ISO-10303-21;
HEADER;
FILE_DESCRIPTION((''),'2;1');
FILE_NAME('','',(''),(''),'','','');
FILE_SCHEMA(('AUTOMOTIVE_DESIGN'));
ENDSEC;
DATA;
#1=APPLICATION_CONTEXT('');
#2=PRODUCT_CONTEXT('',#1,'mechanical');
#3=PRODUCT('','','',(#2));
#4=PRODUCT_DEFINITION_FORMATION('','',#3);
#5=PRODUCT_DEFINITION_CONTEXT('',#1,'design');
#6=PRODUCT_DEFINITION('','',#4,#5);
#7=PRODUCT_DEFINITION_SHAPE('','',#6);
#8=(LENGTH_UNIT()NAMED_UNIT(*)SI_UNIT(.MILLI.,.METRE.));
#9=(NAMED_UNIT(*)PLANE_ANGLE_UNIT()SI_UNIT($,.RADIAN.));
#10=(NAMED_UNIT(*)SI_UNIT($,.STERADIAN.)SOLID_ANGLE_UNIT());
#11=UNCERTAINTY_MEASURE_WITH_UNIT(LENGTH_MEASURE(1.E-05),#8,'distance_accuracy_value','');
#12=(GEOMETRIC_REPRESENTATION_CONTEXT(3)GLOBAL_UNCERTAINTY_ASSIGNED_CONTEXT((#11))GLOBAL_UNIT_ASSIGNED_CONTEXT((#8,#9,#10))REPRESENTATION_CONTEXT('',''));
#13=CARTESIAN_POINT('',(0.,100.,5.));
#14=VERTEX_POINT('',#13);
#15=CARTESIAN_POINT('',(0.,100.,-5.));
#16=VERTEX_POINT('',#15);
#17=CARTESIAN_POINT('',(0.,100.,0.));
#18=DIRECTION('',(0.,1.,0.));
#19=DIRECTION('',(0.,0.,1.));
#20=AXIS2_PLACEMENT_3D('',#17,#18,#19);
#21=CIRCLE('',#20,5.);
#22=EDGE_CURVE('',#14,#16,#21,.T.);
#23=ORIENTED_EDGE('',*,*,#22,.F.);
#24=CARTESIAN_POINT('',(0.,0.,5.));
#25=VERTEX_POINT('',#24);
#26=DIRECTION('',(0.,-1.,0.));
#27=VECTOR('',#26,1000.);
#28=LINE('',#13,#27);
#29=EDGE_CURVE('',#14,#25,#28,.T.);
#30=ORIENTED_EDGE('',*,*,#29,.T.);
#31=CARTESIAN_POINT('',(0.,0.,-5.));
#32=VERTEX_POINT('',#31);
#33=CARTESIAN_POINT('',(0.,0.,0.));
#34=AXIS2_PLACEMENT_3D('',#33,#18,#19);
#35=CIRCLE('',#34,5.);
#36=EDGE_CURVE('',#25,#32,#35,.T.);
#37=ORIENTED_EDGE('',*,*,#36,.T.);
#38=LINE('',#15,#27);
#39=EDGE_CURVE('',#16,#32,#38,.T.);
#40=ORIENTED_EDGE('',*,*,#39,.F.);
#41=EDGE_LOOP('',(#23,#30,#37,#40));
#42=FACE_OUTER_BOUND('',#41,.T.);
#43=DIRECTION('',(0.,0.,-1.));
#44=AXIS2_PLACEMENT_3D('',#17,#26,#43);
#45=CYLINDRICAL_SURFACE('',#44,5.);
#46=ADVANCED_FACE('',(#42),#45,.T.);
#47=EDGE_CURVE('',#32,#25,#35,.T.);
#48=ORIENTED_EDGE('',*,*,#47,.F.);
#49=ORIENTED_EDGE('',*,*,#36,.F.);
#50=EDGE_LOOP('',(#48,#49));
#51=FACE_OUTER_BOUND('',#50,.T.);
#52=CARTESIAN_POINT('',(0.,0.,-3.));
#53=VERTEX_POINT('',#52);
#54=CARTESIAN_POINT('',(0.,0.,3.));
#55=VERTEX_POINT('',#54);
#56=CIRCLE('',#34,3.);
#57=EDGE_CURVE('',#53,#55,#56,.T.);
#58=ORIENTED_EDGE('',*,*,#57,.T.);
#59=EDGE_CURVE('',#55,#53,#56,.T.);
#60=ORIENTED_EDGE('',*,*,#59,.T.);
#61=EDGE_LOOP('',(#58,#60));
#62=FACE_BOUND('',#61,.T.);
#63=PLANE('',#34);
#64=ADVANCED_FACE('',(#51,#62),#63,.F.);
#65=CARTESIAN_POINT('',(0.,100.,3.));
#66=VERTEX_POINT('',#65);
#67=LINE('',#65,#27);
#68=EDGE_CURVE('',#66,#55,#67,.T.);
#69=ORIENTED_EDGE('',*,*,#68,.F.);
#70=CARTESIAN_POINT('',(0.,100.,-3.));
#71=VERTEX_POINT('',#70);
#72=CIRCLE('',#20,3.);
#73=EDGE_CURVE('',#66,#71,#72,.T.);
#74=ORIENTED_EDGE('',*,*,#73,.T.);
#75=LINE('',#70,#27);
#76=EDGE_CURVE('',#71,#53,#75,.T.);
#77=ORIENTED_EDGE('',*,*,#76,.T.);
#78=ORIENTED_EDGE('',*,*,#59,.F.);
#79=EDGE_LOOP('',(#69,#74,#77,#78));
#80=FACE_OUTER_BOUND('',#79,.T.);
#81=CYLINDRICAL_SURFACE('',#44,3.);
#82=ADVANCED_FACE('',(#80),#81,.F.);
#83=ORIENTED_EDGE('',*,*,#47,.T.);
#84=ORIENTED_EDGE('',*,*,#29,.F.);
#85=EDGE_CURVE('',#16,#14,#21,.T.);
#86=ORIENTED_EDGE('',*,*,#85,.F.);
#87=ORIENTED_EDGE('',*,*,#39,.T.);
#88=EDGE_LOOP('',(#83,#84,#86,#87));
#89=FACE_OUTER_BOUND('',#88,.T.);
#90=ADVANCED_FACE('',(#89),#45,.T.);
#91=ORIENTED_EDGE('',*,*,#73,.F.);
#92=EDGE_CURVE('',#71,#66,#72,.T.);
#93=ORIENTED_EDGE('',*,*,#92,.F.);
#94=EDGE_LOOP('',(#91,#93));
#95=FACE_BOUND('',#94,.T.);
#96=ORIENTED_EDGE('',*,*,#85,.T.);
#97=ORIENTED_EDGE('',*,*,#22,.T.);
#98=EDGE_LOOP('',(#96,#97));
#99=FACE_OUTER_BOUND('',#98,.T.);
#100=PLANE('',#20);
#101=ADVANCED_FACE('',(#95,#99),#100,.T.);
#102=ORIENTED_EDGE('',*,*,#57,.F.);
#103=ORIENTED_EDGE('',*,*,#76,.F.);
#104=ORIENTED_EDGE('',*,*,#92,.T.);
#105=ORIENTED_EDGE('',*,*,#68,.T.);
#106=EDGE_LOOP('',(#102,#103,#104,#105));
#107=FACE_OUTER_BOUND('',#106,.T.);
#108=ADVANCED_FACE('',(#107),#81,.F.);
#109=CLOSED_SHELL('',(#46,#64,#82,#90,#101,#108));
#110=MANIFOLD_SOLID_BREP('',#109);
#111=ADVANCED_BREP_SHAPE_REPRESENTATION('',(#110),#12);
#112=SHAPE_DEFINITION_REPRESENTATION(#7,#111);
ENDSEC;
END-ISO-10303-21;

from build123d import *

# Parameters (mm, degrees)
SKETCH_1_R      = 5
SKETCH_1_R_2    = 3
EXTRUDE_1_DEPTH = 100


with BuildPart() as part:
    # 草图1 → 凸台-拉伸1 (new body)
    with BuildSketch(Plane(origin=(0, 0, 0), x_dir=(1, 0, 0), z_dir=(0, 1, 0))):
        with Locations(Location((0, 0, 0), (0, 0, 270))):
            Circle(SKETCH_1_R)
        with Locations(Location((0, 0, 0), (0, 0, 270))):
            Circle(SKETCH_1_R_2, mode=Mode.SUBTRACT)
    extrude(amount=EXTRUDE_1_DEPTH)


solid = part.part
